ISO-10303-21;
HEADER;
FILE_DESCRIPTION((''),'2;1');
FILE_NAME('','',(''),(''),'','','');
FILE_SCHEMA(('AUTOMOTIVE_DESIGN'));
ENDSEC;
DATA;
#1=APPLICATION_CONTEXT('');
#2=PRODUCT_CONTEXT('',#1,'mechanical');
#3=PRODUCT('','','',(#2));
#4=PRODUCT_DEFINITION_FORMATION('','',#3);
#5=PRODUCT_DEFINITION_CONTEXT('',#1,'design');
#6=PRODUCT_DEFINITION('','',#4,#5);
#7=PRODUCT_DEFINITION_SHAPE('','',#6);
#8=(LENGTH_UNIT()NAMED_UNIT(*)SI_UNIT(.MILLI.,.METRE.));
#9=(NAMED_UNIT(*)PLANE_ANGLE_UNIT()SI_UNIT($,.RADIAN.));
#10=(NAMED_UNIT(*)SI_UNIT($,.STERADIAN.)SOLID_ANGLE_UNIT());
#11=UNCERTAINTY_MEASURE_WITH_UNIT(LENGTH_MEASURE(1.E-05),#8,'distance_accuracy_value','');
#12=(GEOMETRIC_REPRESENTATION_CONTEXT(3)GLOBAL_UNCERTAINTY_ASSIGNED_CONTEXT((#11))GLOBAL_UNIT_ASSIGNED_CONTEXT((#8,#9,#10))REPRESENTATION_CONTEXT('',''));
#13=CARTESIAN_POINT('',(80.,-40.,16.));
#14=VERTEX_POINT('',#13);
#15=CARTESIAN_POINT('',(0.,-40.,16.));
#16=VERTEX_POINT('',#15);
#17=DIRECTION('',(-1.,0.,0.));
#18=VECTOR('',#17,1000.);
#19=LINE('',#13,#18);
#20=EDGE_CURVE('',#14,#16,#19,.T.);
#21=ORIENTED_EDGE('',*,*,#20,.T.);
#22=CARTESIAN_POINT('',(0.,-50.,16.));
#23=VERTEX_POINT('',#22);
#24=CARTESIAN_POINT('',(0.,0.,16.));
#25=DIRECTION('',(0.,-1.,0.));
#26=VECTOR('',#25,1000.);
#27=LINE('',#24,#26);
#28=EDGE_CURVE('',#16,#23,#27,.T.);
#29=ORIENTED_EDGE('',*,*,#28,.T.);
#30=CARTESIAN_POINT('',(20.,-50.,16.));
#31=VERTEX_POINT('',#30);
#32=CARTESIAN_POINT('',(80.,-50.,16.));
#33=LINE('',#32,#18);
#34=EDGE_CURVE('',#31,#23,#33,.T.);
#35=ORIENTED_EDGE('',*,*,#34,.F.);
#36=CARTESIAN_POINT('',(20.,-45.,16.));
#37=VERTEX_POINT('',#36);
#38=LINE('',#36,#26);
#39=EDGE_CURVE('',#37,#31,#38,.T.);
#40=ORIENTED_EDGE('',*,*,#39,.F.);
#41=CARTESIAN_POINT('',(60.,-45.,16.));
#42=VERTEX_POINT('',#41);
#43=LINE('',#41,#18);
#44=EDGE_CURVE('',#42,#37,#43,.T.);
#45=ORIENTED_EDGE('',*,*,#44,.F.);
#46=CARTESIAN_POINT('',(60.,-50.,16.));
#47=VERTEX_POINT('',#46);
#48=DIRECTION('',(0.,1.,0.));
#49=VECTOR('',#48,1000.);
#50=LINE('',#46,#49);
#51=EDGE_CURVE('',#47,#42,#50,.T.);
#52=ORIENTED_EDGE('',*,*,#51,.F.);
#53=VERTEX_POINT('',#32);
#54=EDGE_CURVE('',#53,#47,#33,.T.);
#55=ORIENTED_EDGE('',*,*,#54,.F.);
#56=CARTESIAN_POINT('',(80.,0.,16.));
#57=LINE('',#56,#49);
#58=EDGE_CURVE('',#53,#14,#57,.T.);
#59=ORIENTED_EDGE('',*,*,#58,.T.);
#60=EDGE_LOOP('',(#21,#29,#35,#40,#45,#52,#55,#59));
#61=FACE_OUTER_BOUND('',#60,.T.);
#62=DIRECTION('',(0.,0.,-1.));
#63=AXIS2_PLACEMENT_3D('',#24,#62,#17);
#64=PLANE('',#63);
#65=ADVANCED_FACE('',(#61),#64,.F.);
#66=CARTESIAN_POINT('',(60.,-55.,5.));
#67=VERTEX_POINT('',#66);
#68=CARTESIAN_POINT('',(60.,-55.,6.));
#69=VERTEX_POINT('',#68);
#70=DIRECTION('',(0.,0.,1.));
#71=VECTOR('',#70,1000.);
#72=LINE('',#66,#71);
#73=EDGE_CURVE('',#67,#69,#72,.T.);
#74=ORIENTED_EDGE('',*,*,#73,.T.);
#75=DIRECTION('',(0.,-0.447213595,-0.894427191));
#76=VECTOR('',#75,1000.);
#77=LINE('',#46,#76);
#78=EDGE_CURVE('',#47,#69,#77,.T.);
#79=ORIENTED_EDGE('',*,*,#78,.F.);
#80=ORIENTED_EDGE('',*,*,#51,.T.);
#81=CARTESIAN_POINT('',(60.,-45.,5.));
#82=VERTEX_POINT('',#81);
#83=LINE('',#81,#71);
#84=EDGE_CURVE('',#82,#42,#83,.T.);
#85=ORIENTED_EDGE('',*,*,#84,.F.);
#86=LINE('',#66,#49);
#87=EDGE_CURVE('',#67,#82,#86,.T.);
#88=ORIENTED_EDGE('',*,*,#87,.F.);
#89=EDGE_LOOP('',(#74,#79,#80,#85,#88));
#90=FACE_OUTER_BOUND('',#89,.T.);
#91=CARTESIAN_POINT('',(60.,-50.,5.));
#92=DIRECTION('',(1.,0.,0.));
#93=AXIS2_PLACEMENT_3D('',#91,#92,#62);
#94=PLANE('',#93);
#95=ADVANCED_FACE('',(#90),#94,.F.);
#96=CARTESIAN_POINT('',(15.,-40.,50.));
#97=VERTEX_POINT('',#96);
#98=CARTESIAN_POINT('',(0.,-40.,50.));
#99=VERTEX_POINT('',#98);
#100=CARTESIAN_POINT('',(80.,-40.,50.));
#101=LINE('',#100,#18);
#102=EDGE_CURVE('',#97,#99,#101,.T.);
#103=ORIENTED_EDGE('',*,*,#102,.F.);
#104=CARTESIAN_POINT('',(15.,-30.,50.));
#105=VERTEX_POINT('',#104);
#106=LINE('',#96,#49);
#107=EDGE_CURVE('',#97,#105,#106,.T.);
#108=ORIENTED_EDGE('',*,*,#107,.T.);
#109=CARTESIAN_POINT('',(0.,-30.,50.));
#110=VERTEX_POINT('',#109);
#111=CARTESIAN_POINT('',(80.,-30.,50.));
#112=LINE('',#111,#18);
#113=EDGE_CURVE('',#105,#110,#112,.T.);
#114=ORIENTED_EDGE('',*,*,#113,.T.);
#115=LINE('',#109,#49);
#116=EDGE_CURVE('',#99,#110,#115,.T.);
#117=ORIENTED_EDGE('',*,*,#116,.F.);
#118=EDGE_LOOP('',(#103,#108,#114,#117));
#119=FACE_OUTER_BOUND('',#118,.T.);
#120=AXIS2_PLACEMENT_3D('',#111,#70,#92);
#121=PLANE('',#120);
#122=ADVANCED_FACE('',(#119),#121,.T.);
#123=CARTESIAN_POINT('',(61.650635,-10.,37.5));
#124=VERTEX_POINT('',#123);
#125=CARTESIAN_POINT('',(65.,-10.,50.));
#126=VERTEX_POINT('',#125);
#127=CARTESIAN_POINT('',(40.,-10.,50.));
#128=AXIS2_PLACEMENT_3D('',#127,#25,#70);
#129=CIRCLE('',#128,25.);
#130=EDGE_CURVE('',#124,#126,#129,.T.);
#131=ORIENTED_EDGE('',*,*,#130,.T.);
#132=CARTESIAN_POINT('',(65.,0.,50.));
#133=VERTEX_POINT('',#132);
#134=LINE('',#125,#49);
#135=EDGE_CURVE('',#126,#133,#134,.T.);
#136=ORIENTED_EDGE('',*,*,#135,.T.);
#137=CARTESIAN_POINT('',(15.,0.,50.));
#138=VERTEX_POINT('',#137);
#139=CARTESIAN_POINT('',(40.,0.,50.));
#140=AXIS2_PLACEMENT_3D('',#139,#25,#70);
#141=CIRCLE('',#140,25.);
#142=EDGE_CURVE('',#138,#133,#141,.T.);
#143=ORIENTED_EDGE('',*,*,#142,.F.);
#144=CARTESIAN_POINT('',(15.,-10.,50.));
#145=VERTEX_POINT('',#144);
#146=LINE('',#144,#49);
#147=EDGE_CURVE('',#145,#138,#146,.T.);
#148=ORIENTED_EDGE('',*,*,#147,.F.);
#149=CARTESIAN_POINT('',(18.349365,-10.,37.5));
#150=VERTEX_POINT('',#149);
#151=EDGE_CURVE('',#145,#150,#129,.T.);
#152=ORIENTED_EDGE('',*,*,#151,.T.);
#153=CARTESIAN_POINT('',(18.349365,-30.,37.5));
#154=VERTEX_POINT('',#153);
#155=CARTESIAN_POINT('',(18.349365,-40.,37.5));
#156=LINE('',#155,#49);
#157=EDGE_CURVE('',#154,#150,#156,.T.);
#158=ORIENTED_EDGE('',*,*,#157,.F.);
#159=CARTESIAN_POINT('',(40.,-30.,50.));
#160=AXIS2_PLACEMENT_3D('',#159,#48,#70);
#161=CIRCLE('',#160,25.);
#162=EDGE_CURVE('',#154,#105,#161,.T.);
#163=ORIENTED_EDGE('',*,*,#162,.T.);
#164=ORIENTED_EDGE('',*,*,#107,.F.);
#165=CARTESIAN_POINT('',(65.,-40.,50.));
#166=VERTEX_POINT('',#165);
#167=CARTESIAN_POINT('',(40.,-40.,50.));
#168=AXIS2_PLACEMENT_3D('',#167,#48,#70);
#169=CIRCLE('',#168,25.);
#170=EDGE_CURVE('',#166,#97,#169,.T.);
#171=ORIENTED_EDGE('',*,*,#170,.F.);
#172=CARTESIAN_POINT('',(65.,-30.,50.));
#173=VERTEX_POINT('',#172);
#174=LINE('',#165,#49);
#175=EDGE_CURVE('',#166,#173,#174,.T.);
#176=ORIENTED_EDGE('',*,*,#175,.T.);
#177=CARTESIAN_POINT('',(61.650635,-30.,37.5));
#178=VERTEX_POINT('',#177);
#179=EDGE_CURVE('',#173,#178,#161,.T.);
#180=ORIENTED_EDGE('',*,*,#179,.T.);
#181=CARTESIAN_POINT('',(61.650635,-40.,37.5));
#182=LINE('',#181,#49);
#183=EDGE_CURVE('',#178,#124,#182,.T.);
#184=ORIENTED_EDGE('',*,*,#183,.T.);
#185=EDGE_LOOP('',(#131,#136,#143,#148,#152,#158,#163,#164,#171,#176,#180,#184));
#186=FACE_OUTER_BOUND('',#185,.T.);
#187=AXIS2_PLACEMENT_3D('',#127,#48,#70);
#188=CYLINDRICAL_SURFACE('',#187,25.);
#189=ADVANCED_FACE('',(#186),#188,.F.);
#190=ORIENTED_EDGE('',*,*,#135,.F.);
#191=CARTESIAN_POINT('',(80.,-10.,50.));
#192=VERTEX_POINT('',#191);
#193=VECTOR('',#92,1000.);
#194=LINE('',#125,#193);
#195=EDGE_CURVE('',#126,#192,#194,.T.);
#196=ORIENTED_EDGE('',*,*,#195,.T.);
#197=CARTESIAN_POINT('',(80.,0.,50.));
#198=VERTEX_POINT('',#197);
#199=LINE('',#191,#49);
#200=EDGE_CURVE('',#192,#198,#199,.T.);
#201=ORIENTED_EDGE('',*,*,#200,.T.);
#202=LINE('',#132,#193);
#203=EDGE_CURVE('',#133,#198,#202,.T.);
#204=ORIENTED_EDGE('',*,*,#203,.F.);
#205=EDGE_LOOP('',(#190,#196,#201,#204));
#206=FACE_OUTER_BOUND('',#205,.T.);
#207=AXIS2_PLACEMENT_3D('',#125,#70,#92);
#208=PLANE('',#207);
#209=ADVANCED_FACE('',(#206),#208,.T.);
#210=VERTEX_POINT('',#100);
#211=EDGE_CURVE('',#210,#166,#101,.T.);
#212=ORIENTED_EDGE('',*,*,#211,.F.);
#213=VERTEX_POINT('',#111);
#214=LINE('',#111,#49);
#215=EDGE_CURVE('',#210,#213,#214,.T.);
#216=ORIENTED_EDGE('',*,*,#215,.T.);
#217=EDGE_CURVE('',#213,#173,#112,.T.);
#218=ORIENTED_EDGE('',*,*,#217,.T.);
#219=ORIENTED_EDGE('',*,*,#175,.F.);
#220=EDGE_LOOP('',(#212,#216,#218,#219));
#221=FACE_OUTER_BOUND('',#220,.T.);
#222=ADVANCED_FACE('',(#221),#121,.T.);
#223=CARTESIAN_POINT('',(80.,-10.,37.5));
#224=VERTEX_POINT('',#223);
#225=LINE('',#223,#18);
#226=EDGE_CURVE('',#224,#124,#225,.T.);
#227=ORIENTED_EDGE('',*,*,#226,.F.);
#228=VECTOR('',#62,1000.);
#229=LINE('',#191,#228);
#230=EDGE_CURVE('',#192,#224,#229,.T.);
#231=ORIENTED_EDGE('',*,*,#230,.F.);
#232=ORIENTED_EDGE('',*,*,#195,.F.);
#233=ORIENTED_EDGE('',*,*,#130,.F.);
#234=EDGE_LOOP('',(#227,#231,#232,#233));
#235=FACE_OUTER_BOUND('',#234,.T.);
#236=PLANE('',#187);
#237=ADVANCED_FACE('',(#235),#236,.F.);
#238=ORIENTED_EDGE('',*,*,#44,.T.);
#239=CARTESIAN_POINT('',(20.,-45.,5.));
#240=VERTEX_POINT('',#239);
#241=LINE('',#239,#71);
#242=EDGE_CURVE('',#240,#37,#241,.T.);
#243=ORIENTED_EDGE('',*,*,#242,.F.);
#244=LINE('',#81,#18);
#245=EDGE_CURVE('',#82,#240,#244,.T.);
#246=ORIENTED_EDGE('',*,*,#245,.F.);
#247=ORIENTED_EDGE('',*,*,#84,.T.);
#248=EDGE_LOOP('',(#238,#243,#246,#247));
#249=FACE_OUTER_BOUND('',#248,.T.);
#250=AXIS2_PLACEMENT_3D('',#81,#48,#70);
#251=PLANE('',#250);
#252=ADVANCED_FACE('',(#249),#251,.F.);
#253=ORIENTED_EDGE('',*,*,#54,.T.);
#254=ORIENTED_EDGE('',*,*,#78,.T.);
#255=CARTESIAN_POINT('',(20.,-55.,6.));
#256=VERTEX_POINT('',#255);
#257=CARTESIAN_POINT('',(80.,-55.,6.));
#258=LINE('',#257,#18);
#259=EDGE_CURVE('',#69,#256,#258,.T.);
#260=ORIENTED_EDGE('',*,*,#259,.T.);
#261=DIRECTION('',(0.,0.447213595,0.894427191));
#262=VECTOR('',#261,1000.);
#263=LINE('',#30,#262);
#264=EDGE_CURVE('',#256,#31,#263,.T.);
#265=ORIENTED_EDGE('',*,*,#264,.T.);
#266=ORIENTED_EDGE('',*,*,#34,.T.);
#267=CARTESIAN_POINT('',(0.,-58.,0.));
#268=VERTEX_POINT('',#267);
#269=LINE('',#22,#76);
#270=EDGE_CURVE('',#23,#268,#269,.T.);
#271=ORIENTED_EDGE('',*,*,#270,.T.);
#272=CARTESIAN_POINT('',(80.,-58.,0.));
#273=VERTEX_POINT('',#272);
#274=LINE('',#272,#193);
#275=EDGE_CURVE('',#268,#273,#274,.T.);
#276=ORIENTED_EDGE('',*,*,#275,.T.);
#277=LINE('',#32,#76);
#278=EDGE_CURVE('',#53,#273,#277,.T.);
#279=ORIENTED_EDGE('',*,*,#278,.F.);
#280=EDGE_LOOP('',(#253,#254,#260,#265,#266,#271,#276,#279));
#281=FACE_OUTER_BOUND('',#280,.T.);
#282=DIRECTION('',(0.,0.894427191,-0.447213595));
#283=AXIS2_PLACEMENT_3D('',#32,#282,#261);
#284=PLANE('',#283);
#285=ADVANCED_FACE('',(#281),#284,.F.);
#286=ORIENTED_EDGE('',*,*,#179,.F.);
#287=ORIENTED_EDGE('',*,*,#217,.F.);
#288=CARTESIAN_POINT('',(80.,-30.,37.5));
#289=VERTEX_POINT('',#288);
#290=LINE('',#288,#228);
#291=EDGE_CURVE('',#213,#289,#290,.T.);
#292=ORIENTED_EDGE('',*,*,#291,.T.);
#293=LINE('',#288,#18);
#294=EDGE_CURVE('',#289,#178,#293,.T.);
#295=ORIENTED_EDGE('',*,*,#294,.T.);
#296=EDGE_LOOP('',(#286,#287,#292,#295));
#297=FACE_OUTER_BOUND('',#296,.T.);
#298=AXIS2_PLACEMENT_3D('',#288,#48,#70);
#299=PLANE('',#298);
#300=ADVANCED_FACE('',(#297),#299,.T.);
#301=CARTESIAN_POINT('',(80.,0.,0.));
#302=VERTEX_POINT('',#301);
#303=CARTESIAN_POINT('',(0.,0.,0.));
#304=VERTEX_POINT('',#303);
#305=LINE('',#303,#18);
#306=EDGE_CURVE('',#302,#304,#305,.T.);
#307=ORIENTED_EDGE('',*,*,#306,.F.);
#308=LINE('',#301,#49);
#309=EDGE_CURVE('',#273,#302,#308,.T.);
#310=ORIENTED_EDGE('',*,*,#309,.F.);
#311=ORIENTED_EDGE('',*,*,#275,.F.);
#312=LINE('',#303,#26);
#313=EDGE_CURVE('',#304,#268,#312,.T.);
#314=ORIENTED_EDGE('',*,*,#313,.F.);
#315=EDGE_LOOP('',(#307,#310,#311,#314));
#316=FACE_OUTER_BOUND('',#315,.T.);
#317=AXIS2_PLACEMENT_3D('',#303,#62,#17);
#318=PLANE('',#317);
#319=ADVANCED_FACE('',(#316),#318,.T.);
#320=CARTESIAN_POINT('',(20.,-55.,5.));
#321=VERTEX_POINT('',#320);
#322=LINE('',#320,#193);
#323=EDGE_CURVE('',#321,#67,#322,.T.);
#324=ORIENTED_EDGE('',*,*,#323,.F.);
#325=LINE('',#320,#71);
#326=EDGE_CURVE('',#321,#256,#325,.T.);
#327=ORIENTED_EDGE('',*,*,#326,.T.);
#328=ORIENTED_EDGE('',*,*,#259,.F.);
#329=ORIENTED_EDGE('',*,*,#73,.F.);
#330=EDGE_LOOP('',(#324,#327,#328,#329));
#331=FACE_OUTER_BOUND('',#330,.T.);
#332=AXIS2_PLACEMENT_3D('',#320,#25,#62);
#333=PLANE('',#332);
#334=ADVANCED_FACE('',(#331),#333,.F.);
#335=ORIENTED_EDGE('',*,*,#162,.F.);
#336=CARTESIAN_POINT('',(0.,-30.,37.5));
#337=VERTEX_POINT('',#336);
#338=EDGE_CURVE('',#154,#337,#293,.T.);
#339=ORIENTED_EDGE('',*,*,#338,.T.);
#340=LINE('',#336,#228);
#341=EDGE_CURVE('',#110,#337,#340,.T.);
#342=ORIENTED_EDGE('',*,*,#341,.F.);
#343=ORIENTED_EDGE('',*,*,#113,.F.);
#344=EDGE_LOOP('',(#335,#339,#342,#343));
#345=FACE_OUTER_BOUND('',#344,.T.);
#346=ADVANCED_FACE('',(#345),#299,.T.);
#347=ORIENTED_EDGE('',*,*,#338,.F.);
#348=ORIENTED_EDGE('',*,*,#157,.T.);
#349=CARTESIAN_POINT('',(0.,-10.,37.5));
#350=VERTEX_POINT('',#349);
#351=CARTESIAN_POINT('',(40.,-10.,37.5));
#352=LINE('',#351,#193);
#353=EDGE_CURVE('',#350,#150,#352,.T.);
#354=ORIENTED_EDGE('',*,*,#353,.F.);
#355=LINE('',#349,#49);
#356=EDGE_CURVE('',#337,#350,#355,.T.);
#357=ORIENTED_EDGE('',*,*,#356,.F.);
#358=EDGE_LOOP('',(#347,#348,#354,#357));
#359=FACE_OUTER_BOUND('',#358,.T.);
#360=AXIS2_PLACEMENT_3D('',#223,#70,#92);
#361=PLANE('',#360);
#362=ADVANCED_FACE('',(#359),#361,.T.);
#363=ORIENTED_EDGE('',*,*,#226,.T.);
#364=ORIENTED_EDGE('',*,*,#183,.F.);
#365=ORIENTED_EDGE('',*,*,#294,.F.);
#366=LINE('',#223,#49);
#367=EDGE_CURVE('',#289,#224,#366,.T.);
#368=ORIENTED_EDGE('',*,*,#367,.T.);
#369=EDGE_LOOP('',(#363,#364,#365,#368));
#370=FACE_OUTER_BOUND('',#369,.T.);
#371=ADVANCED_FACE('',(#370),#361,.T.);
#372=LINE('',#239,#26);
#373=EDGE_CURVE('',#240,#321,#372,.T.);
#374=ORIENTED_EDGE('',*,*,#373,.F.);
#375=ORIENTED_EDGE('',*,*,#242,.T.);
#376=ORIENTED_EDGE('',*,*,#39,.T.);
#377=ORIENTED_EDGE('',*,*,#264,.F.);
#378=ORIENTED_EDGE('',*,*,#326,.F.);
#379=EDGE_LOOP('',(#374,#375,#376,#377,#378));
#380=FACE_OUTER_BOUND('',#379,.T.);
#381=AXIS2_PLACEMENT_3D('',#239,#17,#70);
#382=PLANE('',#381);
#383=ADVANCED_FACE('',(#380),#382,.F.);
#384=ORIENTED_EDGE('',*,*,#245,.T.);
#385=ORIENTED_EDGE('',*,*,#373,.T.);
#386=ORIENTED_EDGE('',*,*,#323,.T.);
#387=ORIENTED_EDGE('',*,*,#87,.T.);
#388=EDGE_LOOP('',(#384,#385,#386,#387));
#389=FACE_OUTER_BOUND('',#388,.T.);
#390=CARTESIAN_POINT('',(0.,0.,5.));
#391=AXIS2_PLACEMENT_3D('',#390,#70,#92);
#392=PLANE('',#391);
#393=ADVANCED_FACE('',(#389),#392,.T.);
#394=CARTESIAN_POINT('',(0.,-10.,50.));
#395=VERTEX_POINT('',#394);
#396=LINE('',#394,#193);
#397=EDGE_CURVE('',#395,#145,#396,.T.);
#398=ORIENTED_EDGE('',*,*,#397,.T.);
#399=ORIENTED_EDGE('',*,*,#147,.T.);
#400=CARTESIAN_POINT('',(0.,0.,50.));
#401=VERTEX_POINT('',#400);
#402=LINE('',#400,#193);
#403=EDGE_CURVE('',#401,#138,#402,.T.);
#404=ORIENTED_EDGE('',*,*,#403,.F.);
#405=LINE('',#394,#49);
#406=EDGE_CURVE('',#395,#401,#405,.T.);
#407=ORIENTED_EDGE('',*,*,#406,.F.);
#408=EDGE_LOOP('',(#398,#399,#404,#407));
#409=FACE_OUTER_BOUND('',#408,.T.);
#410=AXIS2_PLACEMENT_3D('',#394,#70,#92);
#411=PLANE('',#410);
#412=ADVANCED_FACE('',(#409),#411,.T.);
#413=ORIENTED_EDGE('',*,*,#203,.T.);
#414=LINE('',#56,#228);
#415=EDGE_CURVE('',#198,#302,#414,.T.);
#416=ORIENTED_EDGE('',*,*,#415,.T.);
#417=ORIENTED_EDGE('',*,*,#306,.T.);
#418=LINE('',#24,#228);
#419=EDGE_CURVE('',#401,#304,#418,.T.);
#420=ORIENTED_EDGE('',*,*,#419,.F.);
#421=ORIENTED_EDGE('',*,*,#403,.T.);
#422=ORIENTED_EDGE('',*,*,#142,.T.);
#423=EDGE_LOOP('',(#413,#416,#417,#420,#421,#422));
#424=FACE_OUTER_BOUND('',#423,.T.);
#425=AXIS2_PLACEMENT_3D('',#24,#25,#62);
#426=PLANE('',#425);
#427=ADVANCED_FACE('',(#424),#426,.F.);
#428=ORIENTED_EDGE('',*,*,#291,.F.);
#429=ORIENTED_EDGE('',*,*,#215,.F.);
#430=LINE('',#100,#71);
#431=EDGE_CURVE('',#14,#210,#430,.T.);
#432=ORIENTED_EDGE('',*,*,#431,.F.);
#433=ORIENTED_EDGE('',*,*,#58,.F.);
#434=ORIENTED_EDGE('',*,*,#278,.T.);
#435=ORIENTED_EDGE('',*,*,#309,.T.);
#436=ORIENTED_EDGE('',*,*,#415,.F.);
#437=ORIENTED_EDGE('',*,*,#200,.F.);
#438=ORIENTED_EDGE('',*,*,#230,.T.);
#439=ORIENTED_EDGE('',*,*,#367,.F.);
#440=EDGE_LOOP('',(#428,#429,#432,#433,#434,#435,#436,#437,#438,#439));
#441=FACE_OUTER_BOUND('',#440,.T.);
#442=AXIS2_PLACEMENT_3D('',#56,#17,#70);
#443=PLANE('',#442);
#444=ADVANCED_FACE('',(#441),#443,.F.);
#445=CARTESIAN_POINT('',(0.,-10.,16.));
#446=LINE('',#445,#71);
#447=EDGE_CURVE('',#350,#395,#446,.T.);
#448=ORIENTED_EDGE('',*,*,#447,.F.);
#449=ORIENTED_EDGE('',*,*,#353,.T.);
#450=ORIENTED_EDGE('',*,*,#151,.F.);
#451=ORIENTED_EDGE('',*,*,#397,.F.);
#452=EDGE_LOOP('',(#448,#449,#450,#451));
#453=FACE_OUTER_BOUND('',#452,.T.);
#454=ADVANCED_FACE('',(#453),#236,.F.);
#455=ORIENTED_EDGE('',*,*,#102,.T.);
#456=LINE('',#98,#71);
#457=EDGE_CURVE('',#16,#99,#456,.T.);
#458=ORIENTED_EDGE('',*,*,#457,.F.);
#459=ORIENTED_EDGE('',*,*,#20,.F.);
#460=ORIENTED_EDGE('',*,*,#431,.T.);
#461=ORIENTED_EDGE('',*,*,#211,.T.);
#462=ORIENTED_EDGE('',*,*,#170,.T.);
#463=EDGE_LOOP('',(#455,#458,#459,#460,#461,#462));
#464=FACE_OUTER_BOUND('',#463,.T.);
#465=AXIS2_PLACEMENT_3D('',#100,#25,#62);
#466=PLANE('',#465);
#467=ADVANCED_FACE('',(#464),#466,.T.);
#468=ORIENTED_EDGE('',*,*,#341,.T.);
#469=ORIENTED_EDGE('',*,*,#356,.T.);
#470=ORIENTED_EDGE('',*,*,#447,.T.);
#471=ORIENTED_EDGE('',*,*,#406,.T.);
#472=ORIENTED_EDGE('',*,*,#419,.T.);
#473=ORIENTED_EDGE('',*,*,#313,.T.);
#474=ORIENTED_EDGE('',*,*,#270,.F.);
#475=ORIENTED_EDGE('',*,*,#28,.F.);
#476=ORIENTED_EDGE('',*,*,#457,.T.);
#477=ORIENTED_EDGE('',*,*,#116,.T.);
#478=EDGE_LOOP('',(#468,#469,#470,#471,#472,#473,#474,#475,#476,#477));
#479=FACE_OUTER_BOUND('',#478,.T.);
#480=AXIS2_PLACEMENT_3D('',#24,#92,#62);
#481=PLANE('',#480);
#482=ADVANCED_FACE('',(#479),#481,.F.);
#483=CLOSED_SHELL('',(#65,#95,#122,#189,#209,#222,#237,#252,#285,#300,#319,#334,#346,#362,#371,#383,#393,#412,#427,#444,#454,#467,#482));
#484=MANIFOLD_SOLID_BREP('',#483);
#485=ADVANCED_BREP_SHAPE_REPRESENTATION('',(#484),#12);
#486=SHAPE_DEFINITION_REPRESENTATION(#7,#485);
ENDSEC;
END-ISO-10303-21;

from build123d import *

# Parameters (mm, degrees)
BASE_BLOCK_SKETCH_W        = 80
BASE_BLOCK_SKETCH_H        = 58
BASE_BLOCK_DEPTH           = 16
UPPER_BLOCK_DEPTH          = 10
SIDE_BLOCK_80_DEPTH        = 80
SEMICIRCULAR_BORE_50_DEPTH = 30
RECTANGULAR_SLOT_SKETCH_W  = 43.30127019
RECTANGULAR_SLOT_SKETCH_H  = 12.5
RECTANGULAR_SLOT_DEPTH     = 10
BORE_SIDE_GROOVES_DEPTH    = 10
WEDGE_CUT_DEPTH            = 80
BOTTOM_NOTCH_DEPTH         = 11


with BuildPart() as part:
    # Base Block Sketch → Base Block (new body)
    with BuildSketch(Plane.XY):
        with Locations((40, -29)):
            Rectangle(BASE_BLOCK_SKETCH_W, BASE_BLOCK_SKETCH_H)
    extrude(amount=BASE_BLOCK_DEPTH)

    # Upper Block Sketch → Upper Block (add)
    with BuildSketch(Plane(origin=(0, 0, 0), x_dir=(1, 0, 0), z_dir=(0, 1, 0))):
        with BuildLine():
            Line((0, -16), (0, -50))
            Line((0, -50), (15, -50))
            ThreePointArc((15, -50), (40, -25), (65, -50))
            Line((65, -50), (80, -50))
            Line((80, -50), (80, -16))
            Line((80, -16), (0, -16))
        make_face()
    extrude(amount=-UPPER_BLOCK_DEPTH)

    # Side Block Sketch → Side Block 80 (add)
    with BuildSketch(Plane.ZY):
        Polygon((37.5, -10), (37.5, -30), (50, -30), (50, -40), (16, -40), (16, -10), align=None)
    extrude(amount=-SIDE_BLOCK_80_DEPTH)

    # Bore Ø50 Sketch → Semicircular Bore Ø50 (cut)
    with BuildSketch(Plane(origin=(0, -10, 0), x_dir=(1, 0, 0), z_dir=(0, 1, 0))):
        with BuildLine():
            Line((18.349364905, -37.5), (61.650635095, -37.5))
            ThreePointArc((61.650635095, -37.5), (40, -25), (18.349364905, -37.5))
        make_face()
    extrude(amount=-SEMICIRCULAR_BORE_50_DEPTH, mode=Mode.SUBTRACT)

    # Rectangular Slot Sketch → Rectangular Slot (cut)
    with BuildSketch(Plane.XZ.offset(40)):
        with Locations((40, 43.75)):
            Rectangle(RECTANGULAR_SLOT_SKETCH_W, RECTANGULAR_SLOT_SKETCH_H)
    extrude(amount=-RECTANGULAR_SLOT_DEPTH, mode=Mode.SUBTRACT)

    # Bore Grooves Sketch → Bore Side Grooves (cut)
    with BuildSketch(Plane(origin=(0, -30, 0), x_dir=(1, 0, 0), z_dir=(0, 1, 0))):
        with BuildLine():
            Line((15, -50), (18.349364905, -50))
            Line((18.349364905, -50), (18.349364905, -37.5))
            ThreePointArc((18.349364905, -37.5), (15.851854343, -43.529523872), (15, -50))
        make_face()
        with BuildLine():
            Line((65, -50), (61.650635095, -50))
            Line((61.650635095, -50), (61.650635095, -37.5))
            ThreePointArc((61.650635095, -37.5), (64.148145657, -43.529523872), (65, -50))
        make_face()
    extrude(amount=-BORE_SIDE_GROOVES_DEPTH, mode=Mode.SUBTRACT)

    # Wedge Cut Sketch → Wedge Cut (cut)
    with BuildSketch(Plane.ZY):
        Polygon((16, -50), (0, -58), (16, -58), align=None)
    extrude(amount=-WEDGE_CUT_DEPTH, mode=Mode.SUBTRACT)

    # Bottom Notch Sketch → Bottom Notch (cut)
    with BuildSketch(Plane.XY.offset(16)):
        Polygon((60, -50), (60, -45), (20, -45), (20, -55), (60, -55), align=None)
    extrude(amount=-BOTTOM_NOTCH_DEPTH, mode=Mode.SUBTRACT)


solid = part.part
